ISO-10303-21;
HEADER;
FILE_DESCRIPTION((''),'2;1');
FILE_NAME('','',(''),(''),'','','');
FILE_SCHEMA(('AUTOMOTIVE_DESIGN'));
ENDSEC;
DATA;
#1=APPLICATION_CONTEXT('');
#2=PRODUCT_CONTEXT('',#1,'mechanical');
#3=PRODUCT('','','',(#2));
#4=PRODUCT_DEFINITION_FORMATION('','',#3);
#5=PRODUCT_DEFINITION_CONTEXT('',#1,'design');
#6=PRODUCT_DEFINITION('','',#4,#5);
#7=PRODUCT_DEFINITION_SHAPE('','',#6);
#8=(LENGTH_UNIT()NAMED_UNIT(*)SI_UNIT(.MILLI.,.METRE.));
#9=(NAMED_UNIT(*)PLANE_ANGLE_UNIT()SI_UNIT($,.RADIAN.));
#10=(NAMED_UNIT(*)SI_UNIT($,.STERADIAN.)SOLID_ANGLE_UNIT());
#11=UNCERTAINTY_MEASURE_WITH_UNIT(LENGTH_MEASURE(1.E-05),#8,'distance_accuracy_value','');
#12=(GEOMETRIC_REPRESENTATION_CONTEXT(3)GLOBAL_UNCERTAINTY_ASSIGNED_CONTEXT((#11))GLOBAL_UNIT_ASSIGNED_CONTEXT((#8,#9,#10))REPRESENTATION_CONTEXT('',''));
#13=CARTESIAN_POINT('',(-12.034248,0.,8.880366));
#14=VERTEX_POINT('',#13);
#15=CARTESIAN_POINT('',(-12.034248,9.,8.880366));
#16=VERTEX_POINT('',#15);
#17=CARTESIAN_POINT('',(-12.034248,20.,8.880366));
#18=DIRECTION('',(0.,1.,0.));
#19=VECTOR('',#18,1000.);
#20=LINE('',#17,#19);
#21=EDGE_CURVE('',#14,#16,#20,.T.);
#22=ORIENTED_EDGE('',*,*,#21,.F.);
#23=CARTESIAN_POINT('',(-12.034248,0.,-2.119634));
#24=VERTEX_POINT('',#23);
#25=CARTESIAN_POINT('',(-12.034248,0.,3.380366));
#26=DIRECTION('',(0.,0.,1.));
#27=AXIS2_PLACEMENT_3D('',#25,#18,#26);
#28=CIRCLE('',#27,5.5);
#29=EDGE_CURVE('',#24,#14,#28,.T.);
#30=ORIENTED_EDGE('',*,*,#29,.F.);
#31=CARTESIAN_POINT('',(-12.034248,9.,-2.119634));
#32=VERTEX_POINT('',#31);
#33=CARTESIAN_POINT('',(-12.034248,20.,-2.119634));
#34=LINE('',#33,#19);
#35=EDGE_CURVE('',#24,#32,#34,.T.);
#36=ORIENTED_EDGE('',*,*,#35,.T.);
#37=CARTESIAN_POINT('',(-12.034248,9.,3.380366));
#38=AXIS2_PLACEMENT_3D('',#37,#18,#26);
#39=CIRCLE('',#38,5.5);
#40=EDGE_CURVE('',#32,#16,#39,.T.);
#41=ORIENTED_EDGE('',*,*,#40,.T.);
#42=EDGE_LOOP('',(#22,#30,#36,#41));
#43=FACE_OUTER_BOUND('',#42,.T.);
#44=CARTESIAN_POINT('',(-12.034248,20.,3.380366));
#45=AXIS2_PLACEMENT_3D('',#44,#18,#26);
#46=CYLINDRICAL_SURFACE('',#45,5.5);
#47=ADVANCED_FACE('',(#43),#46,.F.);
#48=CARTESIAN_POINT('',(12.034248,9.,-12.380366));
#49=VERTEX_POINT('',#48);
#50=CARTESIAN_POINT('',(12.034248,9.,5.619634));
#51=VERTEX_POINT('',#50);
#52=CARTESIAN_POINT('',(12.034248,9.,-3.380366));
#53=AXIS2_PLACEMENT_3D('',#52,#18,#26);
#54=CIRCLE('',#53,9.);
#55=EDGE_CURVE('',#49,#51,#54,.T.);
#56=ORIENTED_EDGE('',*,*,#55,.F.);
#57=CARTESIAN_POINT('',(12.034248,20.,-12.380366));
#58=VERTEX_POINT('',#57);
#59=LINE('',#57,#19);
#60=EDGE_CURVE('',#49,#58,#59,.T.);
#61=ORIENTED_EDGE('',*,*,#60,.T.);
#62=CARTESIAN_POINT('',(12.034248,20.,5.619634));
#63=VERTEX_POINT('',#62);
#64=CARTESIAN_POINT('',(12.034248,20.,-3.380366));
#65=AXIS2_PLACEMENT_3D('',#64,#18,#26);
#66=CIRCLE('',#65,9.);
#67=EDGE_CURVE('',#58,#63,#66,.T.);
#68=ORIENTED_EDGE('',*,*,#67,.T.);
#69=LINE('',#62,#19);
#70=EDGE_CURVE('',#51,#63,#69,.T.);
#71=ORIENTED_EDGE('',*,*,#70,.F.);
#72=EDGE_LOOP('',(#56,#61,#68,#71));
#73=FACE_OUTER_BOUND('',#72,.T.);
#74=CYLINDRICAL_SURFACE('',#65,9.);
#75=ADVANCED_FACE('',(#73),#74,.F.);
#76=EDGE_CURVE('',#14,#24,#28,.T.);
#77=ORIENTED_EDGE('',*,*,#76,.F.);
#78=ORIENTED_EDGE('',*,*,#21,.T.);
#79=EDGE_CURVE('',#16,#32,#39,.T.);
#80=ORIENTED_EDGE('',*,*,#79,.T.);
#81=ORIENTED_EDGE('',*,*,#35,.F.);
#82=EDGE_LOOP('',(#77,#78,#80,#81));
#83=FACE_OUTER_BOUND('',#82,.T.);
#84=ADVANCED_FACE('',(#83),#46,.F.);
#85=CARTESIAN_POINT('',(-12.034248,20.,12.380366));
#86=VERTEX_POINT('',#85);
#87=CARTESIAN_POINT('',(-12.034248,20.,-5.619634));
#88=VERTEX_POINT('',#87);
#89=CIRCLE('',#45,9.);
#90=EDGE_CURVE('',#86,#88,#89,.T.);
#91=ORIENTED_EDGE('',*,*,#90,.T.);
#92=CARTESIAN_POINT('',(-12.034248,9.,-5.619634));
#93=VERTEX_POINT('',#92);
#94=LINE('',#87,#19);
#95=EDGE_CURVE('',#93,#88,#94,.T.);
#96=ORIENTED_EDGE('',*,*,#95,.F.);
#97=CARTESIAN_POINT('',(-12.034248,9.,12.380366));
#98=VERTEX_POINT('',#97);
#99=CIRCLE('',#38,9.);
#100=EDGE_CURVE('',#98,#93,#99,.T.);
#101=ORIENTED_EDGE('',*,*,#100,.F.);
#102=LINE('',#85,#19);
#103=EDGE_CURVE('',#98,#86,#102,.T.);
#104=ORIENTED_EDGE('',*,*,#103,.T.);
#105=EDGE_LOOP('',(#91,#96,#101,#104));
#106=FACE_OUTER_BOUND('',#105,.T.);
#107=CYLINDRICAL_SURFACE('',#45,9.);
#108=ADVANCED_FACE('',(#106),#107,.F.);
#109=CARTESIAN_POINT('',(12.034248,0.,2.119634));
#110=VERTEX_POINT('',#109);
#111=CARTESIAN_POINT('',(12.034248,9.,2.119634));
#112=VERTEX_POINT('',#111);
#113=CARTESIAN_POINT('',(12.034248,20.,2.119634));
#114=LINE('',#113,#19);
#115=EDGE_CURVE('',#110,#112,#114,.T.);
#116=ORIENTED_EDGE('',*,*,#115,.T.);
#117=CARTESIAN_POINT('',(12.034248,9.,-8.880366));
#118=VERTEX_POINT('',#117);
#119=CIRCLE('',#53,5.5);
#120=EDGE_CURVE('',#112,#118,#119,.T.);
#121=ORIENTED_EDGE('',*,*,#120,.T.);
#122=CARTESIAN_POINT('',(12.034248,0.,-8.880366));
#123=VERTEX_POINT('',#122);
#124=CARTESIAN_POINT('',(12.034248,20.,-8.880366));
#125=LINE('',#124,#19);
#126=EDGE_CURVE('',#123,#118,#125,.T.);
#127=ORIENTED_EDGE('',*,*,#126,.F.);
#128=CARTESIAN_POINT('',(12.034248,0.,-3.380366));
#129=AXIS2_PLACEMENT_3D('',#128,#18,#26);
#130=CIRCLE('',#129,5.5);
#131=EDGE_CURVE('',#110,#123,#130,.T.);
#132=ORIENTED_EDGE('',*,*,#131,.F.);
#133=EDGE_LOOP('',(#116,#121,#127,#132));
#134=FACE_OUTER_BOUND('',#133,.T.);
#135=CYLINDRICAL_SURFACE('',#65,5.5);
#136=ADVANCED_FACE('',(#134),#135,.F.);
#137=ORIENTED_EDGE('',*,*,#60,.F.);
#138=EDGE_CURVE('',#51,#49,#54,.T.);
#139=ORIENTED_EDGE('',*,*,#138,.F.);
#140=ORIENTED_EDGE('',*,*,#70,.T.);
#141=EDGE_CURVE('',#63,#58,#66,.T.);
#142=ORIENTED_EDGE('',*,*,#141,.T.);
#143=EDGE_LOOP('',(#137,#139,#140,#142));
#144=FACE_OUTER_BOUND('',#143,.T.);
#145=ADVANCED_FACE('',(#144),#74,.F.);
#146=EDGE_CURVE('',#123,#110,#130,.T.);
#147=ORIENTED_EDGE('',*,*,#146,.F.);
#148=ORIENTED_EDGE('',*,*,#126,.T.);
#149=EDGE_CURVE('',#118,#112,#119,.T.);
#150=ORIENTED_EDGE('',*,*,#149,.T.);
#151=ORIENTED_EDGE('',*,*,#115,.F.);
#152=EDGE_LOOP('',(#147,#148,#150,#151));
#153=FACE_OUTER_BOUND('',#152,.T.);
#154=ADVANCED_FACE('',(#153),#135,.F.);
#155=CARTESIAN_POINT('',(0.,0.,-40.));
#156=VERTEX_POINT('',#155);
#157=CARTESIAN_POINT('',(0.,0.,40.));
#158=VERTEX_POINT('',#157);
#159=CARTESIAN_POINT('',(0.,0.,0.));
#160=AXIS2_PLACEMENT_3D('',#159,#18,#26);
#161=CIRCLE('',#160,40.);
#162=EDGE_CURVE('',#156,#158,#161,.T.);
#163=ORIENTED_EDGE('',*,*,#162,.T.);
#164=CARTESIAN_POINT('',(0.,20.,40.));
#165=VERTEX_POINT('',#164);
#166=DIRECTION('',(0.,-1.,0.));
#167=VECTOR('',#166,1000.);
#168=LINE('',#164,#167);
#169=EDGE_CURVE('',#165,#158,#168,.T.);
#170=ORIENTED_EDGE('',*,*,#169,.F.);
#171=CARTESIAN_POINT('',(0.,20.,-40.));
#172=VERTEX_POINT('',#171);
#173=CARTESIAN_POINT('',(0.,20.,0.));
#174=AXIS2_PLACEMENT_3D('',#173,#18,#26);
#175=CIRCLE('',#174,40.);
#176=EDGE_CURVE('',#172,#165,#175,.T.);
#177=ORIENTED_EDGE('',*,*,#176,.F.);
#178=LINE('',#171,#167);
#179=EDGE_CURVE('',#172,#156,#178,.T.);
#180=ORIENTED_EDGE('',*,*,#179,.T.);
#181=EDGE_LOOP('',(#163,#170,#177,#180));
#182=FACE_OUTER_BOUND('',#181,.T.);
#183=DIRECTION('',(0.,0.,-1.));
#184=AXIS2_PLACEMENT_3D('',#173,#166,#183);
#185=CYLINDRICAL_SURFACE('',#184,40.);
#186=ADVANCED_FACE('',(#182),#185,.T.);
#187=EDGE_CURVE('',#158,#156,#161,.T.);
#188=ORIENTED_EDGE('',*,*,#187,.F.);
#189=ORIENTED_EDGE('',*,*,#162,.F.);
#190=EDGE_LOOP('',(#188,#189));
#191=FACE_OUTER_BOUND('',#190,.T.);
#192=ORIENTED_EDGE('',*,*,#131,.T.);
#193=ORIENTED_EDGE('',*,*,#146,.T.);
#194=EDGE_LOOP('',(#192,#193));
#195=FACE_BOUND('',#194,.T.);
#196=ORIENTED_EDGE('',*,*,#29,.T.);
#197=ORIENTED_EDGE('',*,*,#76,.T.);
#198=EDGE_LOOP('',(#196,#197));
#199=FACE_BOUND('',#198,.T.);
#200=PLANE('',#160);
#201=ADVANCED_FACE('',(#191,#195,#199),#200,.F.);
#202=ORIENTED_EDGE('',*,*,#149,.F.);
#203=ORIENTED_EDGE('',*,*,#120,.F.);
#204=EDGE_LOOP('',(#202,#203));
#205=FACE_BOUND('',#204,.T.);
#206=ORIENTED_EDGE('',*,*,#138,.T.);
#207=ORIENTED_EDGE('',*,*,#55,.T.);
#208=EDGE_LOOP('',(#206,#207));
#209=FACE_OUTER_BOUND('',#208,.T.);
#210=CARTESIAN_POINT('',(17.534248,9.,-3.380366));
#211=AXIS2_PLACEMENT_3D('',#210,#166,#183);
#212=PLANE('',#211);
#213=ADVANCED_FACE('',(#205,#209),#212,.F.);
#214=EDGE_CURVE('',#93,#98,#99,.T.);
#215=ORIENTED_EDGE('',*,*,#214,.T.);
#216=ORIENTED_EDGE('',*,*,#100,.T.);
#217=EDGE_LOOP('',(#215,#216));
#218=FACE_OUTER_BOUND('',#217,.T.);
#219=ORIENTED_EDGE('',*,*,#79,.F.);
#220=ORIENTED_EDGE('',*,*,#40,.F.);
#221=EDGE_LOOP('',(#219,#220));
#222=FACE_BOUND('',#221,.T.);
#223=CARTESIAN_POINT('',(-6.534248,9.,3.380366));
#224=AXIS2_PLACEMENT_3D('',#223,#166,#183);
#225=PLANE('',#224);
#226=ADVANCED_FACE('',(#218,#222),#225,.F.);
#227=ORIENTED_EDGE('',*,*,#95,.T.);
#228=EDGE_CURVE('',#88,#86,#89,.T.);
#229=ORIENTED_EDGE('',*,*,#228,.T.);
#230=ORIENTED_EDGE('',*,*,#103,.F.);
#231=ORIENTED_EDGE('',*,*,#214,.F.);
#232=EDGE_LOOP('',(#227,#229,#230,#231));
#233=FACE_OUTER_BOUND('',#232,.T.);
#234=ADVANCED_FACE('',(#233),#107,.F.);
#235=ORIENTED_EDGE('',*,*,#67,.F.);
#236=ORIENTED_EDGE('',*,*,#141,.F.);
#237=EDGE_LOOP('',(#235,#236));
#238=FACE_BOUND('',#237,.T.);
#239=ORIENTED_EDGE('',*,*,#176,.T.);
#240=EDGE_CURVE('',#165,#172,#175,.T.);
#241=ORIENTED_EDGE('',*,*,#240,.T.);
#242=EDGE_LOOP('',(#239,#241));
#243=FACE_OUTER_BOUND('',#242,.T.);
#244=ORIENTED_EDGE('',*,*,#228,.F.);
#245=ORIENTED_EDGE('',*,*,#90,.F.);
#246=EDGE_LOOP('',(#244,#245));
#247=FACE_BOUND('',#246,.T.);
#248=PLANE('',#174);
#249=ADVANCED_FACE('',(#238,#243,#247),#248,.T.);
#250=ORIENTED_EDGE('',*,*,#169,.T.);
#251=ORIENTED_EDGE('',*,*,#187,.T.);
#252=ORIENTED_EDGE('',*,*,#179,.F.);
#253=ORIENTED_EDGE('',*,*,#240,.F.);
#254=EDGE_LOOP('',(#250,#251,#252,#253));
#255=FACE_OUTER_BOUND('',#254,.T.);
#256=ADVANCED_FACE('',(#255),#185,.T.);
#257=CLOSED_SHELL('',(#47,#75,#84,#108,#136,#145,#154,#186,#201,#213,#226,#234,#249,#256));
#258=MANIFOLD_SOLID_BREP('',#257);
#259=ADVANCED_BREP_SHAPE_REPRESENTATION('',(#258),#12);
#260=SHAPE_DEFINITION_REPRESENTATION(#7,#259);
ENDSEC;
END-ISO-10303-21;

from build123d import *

# Parameters (mm, degrees)
SKETCH1_R                                           = 40
BOSS_EXTRUDE1_DEPTH                                 = 20
HOLE_SIZE_PER_SOCKET_HEAD_CAP_SCREW_TYP_D           = 11
HOLE_SIZE_PER_SOCKET_HEAD_CAP_SCREW_TYP_CBORE_D     = 18
HOLE_SIZE_PER_SOCKET_HEAD_CAP_SCREW_TYP_CBORE_DEPTH = 11


with BuildPart() as part:
    # Sketch1 → Boss-Extrude1 (new body)
    with BuildSketch(Plane(origin=(0, 0, 0), x_dir=(1, 0, 0), z_dir=(0, 1, 0))):
        with Locations(Location((0, 0, 0), (0, 0, 270))):
            Circle(SKETCH1_R)
    extrude(amount=BOSS_EXTRUDE1_DEPTH)

    # Hole size (per socket head cap screw type) 1 (through all)
    with Locations(Plane(origin=(-12.034248035, 20, 3.380365992), x_dir=(0, 0, 1), z_dir=(0, 1, 0))):
        with Locations((0, 0), (-6.760731984, 24.06849607)):
            CounterBoreHole(HOLE_SIZE_PER_SOCKET_HEAD_CAP_SCREW_TYP_D / 2, HOLE_SIZE_PER_SOCKET_HEAD_CAP_SCREW_TYP_CBORE_D / 2, HOLE_SIZE_PER_SOCKET_HEAD_CAP_SCREW_TYP_CBORE_DEPTH)


solid = part.part
